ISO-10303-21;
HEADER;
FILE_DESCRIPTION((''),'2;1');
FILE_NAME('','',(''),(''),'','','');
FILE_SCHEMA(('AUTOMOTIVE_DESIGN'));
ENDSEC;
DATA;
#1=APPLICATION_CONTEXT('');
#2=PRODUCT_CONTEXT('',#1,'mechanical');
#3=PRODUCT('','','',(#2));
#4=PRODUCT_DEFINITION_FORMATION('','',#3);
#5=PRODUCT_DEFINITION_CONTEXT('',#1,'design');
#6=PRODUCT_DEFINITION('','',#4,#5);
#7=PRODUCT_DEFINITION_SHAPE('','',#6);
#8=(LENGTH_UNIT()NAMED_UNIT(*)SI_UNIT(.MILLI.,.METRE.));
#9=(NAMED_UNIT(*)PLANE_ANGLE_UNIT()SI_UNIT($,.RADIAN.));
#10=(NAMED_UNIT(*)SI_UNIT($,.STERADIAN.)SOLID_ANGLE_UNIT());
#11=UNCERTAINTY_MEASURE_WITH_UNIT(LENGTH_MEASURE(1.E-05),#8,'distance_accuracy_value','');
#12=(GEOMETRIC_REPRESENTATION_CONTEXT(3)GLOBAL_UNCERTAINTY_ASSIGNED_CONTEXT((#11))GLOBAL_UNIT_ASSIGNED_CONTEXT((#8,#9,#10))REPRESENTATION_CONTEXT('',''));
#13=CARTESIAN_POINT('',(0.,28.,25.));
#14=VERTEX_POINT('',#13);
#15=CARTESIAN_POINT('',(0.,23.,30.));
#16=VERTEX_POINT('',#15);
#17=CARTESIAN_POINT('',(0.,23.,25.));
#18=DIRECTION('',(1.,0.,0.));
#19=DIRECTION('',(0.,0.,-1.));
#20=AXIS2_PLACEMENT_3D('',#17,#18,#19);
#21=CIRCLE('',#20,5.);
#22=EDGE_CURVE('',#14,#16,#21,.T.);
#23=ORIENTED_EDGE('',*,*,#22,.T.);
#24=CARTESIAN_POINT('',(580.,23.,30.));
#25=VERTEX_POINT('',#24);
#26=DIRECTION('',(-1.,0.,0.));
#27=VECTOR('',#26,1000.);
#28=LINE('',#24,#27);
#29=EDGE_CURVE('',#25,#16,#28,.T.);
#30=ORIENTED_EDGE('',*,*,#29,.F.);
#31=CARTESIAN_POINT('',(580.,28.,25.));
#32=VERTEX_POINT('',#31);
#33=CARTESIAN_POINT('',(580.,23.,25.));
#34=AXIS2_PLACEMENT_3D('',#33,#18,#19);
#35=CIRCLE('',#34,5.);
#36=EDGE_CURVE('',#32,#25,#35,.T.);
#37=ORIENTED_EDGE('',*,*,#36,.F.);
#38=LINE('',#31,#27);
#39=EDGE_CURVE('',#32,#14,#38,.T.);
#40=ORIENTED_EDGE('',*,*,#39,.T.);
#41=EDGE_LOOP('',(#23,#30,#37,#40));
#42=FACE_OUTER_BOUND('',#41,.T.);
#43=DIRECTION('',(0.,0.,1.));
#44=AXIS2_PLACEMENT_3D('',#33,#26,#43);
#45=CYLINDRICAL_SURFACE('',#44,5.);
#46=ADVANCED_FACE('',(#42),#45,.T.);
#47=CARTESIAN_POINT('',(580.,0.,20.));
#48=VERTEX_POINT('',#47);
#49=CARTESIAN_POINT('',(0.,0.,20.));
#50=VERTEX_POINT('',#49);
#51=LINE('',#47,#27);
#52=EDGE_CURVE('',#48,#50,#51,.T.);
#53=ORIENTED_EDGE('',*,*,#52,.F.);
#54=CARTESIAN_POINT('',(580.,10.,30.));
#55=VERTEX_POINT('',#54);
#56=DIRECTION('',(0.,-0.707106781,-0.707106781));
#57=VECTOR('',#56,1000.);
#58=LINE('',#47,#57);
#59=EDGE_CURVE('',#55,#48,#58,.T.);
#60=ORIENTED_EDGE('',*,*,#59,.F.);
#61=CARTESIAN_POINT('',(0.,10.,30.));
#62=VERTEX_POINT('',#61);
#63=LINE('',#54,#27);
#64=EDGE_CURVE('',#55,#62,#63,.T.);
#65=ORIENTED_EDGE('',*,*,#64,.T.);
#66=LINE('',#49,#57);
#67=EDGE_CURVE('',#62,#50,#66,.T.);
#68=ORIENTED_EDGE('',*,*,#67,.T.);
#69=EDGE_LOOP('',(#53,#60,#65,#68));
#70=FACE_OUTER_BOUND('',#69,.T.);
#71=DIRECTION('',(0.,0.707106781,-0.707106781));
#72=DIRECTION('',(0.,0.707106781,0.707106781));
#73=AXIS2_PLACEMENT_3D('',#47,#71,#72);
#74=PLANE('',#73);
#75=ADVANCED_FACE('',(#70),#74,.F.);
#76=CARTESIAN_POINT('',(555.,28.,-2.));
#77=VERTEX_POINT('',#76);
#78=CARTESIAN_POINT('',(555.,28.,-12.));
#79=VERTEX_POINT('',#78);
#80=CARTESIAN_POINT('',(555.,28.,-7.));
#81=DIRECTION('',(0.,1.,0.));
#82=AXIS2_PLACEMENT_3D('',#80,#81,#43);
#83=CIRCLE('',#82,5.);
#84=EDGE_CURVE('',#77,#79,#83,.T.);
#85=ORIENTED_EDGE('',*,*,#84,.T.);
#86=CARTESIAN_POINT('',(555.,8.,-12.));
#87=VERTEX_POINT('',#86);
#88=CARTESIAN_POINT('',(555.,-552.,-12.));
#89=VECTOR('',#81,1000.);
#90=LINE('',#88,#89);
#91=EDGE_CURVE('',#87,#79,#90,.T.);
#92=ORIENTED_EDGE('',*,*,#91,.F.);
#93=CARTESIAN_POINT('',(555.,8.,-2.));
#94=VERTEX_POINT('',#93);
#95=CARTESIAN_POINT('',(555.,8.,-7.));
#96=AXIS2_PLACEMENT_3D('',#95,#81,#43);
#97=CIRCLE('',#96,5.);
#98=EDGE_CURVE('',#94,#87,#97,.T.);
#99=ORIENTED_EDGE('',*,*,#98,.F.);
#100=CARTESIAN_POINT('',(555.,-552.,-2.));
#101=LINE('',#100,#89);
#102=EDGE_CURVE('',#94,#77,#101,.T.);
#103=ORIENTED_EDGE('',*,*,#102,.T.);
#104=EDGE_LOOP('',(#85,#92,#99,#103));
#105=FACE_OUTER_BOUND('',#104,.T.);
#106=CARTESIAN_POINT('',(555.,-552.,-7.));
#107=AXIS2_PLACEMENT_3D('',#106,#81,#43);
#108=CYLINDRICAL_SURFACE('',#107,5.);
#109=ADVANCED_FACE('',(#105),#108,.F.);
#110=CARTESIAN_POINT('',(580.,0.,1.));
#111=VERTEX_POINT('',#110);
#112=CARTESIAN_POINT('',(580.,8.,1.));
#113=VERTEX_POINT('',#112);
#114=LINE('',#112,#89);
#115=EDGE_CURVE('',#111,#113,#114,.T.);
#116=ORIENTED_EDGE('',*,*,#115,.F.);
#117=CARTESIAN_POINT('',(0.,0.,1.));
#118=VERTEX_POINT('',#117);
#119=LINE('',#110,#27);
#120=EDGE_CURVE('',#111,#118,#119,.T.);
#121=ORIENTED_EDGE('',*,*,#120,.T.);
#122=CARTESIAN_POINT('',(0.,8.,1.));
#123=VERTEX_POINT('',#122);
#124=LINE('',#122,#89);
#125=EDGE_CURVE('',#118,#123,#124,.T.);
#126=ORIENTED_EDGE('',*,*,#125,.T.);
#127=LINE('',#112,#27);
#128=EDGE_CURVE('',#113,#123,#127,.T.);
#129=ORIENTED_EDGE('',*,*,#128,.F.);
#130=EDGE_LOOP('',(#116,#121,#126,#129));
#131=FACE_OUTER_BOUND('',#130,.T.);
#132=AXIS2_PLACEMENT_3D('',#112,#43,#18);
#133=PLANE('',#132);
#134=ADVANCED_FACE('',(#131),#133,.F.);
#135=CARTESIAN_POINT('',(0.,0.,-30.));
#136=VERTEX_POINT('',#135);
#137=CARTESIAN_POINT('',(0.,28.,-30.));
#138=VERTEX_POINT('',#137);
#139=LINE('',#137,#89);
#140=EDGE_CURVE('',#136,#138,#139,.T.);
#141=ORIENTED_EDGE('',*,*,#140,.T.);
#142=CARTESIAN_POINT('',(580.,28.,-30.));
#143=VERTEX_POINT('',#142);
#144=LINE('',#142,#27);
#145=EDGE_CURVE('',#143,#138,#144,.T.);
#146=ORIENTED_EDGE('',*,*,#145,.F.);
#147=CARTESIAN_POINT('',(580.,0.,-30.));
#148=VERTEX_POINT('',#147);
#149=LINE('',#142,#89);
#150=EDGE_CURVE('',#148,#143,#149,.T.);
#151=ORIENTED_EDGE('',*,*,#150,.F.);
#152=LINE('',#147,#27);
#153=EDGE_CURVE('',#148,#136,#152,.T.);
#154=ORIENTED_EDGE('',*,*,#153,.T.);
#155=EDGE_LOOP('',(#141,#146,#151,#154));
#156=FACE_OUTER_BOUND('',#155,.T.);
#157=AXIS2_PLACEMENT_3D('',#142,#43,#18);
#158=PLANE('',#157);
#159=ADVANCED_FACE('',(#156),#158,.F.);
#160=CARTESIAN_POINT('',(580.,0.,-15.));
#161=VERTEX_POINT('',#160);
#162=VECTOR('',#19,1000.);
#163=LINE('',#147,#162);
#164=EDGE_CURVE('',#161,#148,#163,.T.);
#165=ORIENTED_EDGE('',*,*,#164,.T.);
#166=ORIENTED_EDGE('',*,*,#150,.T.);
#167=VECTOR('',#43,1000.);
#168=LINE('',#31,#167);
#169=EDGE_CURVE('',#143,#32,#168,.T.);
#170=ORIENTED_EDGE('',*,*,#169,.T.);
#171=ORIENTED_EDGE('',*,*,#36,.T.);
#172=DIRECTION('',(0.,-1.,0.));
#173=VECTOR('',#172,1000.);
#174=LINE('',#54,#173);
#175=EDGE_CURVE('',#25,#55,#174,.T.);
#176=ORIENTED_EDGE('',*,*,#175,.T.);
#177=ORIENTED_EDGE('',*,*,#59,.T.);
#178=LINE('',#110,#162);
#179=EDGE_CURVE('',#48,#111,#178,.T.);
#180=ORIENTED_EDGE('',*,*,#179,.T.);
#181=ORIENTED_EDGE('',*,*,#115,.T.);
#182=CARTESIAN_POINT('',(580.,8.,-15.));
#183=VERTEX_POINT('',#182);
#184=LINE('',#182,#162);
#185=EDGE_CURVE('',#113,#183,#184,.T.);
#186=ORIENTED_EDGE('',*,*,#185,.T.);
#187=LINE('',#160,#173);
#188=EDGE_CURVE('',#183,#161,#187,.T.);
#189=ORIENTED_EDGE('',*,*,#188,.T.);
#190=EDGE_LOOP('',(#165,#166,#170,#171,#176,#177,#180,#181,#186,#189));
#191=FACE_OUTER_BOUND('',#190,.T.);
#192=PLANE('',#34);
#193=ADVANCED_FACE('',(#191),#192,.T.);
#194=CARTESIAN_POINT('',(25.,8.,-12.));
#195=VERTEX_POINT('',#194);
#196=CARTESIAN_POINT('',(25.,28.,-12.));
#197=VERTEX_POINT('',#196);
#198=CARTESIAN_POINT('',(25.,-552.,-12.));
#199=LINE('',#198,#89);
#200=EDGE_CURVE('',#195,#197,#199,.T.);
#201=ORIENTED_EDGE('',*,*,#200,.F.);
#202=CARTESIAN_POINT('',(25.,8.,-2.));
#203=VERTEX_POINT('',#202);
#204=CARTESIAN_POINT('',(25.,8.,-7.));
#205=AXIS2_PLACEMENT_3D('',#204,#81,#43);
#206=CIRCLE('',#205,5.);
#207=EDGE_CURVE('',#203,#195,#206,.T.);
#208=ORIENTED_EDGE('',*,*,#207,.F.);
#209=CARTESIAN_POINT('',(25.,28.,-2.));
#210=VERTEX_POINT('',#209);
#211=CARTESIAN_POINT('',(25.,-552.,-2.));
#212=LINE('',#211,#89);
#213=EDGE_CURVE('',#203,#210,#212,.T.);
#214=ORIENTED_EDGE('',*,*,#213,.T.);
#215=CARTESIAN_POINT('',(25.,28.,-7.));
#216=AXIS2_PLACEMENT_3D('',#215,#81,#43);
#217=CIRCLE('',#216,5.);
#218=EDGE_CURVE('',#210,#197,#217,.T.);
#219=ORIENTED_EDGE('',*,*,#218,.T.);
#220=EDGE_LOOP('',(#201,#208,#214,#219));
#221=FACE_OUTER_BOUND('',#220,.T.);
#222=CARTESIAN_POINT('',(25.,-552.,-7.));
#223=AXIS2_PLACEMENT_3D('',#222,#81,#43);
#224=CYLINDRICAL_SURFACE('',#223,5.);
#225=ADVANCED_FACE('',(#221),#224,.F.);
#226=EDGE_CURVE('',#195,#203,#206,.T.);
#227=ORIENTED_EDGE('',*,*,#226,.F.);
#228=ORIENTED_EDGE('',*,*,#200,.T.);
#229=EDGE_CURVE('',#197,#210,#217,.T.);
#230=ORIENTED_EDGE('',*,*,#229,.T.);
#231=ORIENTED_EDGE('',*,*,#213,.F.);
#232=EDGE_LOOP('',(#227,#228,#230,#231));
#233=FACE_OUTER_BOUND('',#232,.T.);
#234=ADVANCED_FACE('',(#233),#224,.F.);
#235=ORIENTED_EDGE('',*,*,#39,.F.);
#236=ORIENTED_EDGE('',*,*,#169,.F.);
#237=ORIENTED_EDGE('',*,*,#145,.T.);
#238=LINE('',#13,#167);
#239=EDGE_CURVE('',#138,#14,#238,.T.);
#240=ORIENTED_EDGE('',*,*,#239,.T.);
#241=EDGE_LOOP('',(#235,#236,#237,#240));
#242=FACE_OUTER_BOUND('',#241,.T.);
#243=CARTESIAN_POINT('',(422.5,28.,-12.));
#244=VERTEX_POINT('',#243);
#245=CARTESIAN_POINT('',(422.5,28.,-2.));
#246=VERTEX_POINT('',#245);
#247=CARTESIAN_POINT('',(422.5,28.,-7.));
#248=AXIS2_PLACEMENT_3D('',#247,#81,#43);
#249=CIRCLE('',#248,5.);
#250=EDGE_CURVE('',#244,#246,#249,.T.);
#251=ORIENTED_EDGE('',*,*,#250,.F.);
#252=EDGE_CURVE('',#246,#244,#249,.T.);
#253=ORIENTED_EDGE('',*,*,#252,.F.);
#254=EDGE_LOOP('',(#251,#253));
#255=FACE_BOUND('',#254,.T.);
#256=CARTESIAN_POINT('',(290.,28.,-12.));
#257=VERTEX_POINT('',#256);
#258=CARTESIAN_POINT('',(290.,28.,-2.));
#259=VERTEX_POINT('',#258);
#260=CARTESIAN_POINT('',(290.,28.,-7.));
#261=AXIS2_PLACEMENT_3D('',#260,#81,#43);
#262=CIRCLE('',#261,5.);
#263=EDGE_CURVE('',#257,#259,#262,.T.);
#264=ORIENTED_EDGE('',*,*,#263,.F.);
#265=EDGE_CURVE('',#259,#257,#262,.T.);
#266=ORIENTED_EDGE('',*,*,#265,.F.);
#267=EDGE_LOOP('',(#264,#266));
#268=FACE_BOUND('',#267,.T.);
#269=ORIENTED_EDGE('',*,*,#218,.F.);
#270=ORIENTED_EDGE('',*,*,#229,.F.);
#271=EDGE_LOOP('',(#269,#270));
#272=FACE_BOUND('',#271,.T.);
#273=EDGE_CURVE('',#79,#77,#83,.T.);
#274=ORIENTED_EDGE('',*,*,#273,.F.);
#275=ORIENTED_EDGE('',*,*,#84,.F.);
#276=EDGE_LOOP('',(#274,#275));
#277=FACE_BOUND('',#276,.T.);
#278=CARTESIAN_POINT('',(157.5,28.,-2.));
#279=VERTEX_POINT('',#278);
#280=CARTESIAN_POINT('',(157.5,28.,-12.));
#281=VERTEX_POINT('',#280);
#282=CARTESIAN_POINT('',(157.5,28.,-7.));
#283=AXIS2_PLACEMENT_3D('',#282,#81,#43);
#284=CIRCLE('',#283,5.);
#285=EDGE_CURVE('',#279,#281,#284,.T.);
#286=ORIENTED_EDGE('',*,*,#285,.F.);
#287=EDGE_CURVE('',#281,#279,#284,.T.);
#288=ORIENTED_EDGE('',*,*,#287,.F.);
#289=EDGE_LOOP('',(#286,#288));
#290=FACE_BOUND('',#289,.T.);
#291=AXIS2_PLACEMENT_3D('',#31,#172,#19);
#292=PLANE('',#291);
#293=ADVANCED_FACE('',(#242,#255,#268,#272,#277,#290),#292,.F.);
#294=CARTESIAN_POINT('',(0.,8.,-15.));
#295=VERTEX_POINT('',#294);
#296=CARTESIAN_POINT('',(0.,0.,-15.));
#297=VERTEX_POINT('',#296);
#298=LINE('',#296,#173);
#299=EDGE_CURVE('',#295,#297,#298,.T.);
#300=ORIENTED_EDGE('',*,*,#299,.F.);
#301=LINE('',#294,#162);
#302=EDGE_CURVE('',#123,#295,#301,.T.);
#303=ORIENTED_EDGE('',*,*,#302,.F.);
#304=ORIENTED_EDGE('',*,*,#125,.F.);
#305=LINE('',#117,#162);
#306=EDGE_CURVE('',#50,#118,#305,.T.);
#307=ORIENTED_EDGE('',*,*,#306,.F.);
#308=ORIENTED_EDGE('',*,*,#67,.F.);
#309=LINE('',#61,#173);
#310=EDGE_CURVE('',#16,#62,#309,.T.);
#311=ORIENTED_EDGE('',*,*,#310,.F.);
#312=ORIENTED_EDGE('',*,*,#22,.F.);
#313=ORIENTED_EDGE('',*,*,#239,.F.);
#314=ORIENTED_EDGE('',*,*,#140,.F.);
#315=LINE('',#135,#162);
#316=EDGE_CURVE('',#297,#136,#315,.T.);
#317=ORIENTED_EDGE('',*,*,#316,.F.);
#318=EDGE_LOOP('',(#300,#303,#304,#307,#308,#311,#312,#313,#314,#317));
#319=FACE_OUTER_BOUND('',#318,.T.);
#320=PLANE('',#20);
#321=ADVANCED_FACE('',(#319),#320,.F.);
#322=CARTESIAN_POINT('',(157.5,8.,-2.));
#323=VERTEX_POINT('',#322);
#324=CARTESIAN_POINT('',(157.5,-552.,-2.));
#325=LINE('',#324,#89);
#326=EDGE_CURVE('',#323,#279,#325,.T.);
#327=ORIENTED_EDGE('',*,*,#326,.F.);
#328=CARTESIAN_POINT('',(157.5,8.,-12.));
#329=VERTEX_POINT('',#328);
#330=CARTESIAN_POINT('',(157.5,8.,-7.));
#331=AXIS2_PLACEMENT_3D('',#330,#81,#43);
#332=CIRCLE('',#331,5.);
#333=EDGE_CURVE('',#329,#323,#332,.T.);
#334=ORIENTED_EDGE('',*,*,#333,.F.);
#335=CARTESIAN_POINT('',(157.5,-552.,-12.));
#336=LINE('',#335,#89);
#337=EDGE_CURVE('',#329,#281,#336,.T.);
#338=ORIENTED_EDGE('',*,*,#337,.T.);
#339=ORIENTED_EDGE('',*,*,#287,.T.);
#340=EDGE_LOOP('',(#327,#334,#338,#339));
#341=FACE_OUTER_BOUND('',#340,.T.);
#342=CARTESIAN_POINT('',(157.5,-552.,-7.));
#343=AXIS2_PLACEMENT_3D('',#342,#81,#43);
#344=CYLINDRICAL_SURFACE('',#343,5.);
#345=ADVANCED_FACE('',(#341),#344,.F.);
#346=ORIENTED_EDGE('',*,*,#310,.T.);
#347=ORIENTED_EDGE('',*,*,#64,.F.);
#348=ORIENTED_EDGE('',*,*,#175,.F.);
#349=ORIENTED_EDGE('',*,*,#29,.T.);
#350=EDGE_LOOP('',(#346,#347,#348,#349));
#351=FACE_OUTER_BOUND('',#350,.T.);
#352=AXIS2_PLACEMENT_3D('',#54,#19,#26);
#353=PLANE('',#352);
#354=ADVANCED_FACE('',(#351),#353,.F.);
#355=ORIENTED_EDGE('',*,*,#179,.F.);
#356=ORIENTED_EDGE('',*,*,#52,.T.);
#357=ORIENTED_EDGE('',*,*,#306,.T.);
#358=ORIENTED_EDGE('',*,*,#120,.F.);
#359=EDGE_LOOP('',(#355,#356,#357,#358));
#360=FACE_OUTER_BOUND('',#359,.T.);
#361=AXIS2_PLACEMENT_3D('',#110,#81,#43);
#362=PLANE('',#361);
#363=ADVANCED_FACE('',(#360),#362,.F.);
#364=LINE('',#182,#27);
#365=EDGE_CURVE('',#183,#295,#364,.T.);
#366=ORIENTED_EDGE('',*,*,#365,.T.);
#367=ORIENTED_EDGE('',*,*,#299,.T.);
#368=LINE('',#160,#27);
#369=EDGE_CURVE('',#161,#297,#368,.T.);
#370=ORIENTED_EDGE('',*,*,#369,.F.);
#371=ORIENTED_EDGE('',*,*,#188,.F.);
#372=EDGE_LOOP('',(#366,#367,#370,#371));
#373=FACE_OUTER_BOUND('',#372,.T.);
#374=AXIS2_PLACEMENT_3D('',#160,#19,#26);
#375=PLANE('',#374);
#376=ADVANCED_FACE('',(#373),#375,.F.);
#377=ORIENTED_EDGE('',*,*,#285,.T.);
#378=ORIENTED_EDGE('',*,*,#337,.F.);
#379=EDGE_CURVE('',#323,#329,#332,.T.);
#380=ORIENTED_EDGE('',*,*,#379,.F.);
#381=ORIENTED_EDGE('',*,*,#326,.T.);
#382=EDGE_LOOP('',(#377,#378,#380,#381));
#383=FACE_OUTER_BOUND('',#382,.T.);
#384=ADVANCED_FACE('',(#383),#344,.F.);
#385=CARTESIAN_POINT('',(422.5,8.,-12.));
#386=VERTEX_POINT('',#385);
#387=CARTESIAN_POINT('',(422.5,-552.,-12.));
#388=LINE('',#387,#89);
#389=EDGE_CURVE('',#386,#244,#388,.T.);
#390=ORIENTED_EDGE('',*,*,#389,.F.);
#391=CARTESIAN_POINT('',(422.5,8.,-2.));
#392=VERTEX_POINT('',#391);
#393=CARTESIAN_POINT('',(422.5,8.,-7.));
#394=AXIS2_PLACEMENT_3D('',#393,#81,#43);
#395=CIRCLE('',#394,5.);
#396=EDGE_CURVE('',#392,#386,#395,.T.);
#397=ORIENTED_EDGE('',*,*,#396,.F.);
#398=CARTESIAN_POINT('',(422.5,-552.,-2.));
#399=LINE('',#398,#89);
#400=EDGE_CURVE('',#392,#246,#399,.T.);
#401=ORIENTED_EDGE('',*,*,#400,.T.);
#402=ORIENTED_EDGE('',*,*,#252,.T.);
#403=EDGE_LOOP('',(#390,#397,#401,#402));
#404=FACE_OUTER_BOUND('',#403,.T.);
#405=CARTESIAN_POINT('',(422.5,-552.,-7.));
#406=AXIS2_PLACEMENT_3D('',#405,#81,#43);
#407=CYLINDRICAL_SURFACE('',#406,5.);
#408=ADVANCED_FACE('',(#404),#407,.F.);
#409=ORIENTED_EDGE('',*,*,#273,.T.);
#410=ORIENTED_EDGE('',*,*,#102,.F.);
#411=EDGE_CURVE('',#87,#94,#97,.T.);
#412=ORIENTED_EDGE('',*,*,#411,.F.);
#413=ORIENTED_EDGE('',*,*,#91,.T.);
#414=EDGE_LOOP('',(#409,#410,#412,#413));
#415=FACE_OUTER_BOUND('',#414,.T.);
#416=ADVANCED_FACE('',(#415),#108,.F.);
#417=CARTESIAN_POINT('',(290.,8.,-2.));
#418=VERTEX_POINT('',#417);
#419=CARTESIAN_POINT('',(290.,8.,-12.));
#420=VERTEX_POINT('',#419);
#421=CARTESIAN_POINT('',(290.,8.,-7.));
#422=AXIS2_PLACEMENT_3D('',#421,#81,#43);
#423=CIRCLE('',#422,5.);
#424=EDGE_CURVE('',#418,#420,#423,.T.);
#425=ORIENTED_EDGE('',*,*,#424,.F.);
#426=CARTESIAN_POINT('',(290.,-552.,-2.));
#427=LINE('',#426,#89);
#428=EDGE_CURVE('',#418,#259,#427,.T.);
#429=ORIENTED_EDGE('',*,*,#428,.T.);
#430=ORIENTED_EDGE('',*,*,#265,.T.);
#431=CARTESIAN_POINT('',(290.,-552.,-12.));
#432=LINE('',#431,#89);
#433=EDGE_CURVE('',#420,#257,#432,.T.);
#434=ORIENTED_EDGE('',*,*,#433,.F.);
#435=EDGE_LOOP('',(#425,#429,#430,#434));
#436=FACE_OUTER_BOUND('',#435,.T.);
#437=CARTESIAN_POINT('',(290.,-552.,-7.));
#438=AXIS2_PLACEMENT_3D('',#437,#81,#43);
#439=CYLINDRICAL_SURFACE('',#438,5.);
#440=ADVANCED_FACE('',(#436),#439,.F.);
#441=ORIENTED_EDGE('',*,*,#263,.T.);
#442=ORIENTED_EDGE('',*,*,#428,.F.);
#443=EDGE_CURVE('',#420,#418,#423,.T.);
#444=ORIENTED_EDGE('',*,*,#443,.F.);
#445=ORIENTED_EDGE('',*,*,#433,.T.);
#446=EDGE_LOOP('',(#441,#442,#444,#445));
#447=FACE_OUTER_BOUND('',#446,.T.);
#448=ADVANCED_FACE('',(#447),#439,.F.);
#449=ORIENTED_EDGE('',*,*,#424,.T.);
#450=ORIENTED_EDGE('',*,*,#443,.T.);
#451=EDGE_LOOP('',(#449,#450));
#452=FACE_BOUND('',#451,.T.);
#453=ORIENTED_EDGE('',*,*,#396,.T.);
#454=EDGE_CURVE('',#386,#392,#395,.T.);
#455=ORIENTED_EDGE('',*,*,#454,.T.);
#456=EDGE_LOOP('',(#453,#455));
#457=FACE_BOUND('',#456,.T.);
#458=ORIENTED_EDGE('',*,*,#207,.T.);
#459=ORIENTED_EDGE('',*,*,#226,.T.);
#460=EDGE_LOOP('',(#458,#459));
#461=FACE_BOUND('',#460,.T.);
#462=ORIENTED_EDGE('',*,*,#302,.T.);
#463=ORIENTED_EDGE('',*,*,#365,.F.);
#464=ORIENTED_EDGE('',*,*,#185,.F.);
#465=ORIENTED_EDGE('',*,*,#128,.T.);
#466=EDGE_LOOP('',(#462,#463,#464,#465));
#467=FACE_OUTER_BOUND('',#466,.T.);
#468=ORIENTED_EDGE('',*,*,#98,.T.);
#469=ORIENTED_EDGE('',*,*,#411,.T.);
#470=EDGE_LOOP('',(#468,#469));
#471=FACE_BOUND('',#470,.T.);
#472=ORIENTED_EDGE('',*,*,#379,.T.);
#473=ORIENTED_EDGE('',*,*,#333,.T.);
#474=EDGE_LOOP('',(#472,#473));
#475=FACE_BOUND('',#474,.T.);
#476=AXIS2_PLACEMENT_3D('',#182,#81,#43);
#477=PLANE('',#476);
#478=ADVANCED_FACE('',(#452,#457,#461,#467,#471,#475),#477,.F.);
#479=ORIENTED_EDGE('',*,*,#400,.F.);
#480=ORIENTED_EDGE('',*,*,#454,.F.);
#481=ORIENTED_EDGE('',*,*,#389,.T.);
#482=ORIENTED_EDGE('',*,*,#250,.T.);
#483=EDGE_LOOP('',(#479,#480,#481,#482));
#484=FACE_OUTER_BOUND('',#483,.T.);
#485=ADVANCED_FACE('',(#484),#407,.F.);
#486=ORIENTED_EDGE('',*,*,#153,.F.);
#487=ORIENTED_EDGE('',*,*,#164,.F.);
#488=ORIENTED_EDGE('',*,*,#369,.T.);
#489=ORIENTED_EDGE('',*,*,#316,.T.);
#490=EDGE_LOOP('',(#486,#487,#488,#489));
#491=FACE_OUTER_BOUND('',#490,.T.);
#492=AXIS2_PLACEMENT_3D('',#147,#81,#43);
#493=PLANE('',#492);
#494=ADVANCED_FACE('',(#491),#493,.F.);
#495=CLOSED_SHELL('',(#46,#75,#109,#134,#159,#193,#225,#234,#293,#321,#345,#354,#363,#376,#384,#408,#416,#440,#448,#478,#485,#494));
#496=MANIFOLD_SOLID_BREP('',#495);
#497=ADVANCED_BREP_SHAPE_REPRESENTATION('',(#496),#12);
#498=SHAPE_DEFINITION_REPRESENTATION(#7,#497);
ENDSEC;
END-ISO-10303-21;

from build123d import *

# Parameters (mm, degrees)
RAIL_BODY_580_DEPTH        = 580
MOUNTING_HOLES_SKETCH_R    = 5
MOUNTING_HOLES_5X_10_DEPTH = 580


with BuildPart() as part:
    # Rail Profile Sketch → Rail Body 580 (new body)
    with BuildSketch(Plane(origin=(0, 0, 0), x_dir=(0, 0, -1), z_dir=(1, 0, 0))):
        with BuildLine():
            Line((-30, 10), (-30, 23))
            ThreePointArc((-30, 23), (-28.535533906, 26.535533906), (-25, 28))
            Line((-25, 28), (30, 28))
            Line((30, 28), (30, 0))
            Line((30, 0), (15, 0))
            Line((15, 0), (15, 8))
            Line((15, 8), (-1, 8))
            Line((-1, 8), (-1, 0))
            Line((-1, 0), (-20, 0))
            Line((-20, 0), (-30, 10))
        make_face()
    extrude(amount=RAIL_BODY_580_DEPTH)

    # Mounting Holes Sketch → Mounting Holes 5xØ10 (cut)
    with BuildSketch(Plane(origin=(0, 28, 0), x_dir=(1, 0, 0), z_dir=(0, 1, 0))):
        with Locations(Location((25, 7, 0), (0, 0, 270))):
            Circle(MOUNTING_HOLES_SKETCH_R)
        with Locations(Location((157.5, 7, 0), (0, 0, 270))):
            Circle(MOUNTING_HOLES_SKETCH_R)
        with Locations(Location((290, 7, 0), (0, 0, 270))):
            Circle(MOUNTING_HOLES_SKETCH_R)
        with Locations(Location((422.5, 7, 0), (0, 0, 270))):
            Circle(MOUNTING_HOLES_SKETCH_R)
        with Locations(Location((555, 7, 0), (0, 0, 270))):
            Circle(MOUNTING_HOLES_SKETCH_R)
    extrude(amount=-MOUNTING_HOLES_5X_10_DEPTH, mode=Mode.SUBTRACT)


solid = part.part
